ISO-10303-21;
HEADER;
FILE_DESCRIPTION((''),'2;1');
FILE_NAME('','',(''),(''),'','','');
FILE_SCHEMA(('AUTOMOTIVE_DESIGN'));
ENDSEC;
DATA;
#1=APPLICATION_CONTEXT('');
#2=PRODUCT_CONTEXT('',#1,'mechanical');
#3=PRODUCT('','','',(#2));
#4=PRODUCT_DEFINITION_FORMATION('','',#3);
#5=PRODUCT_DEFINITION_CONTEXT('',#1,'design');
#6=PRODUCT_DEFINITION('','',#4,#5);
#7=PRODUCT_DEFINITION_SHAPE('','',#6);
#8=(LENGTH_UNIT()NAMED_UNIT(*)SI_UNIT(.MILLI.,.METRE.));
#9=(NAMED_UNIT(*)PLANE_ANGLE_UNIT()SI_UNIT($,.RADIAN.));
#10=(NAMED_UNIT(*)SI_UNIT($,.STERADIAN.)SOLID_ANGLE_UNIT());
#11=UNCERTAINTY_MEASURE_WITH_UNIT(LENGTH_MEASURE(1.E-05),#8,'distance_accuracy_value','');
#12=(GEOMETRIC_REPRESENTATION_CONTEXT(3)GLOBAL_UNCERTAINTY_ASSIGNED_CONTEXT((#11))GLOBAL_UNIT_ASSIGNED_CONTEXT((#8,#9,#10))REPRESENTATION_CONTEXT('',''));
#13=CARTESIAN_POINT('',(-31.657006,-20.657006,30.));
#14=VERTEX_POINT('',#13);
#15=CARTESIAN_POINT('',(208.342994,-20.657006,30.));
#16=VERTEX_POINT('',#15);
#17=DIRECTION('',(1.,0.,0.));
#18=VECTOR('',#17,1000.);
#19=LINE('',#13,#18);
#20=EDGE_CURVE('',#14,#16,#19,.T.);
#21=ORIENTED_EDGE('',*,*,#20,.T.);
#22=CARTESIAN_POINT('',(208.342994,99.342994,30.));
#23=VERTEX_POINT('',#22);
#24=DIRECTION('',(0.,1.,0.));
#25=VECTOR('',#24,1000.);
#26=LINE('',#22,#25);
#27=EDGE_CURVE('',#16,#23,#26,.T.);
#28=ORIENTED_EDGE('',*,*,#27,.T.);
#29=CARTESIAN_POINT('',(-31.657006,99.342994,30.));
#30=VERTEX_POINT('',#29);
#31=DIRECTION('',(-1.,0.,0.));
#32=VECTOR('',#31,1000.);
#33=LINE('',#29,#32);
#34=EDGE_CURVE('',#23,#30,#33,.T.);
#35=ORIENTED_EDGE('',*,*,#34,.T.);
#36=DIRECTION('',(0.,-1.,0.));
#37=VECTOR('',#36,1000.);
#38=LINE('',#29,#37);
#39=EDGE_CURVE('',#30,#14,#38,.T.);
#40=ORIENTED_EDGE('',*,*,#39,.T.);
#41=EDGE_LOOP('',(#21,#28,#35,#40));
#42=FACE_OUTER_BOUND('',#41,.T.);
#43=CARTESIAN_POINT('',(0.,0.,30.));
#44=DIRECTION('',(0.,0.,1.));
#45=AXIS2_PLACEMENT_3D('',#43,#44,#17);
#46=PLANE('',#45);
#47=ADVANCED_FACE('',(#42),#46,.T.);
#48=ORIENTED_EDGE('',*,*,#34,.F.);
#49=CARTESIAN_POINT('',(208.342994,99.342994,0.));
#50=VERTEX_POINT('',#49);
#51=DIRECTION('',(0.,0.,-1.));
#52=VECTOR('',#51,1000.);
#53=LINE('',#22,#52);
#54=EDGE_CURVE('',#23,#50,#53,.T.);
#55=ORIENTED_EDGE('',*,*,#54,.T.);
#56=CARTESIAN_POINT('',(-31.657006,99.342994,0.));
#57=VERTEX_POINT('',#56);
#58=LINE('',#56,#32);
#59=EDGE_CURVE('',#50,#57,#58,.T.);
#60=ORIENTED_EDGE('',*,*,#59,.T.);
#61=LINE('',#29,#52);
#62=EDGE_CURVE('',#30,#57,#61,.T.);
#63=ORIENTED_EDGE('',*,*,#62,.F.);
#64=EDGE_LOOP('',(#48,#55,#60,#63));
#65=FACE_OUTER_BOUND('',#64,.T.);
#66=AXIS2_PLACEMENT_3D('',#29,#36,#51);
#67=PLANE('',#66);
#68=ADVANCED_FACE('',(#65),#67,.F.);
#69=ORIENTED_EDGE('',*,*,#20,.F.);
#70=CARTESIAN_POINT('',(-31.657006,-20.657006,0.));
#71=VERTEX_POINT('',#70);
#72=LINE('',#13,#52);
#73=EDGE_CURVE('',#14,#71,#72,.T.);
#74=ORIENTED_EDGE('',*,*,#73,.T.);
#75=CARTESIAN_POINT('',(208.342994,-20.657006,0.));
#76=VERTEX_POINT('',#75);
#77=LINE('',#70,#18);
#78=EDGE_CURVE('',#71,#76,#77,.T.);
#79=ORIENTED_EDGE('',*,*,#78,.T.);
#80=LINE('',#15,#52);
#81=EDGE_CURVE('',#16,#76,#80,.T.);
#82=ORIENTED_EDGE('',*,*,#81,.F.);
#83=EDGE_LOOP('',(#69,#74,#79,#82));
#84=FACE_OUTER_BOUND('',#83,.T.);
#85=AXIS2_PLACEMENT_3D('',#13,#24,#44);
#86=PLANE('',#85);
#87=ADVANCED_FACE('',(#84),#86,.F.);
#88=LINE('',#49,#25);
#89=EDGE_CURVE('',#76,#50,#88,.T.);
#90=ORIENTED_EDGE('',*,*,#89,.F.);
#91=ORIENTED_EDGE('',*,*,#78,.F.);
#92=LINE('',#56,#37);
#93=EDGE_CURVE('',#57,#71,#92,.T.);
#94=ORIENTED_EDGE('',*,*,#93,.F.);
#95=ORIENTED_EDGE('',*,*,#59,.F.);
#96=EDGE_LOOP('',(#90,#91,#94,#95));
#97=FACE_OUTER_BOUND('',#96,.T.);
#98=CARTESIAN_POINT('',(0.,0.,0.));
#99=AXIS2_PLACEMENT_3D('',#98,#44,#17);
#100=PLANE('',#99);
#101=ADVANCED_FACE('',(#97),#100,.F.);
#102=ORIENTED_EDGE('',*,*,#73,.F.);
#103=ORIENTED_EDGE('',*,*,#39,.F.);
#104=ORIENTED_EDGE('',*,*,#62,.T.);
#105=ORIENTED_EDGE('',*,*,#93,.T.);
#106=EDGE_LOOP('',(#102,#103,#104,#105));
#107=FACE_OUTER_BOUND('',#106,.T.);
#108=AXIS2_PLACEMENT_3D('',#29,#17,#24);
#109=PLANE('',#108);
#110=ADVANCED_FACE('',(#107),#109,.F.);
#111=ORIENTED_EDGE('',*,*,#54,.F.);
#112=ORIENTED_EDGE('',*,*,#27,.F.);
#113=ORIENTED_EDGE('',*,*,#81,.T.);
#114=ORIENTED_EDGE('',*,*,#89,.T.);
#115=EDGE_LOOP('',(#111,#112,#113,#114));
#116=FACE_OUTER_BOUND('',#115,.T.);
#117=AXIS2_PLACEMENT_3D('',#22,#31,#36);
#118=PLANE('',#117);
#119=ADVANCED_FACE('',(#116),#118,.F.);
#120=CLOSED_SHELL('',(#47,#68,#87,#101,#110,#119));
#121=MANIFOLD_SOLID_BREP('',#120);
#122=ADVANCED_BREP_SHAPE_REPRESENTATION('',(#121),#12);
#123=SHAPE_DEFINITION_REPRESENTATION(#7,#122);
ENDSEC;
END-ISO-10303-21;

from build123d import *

# Parameters (mm, degrees)
SKETCH1_W           = 240
SKETCH1_H           = 120
BOSS_EXTRUDE1_DEPTH = 30


with BuildPart() as part:
    # Sketch1 → Boss-Extrude1 (new body)
    with BuildSketch(Plane.XY):
        with Locations((88.34299394, 39.34299394)):
            Rectangle(SKETCH1_W, SKETCH1_H)
    extrude(amount=BOSS_EXTRUDE1_DEPTH)


solid = part.part
